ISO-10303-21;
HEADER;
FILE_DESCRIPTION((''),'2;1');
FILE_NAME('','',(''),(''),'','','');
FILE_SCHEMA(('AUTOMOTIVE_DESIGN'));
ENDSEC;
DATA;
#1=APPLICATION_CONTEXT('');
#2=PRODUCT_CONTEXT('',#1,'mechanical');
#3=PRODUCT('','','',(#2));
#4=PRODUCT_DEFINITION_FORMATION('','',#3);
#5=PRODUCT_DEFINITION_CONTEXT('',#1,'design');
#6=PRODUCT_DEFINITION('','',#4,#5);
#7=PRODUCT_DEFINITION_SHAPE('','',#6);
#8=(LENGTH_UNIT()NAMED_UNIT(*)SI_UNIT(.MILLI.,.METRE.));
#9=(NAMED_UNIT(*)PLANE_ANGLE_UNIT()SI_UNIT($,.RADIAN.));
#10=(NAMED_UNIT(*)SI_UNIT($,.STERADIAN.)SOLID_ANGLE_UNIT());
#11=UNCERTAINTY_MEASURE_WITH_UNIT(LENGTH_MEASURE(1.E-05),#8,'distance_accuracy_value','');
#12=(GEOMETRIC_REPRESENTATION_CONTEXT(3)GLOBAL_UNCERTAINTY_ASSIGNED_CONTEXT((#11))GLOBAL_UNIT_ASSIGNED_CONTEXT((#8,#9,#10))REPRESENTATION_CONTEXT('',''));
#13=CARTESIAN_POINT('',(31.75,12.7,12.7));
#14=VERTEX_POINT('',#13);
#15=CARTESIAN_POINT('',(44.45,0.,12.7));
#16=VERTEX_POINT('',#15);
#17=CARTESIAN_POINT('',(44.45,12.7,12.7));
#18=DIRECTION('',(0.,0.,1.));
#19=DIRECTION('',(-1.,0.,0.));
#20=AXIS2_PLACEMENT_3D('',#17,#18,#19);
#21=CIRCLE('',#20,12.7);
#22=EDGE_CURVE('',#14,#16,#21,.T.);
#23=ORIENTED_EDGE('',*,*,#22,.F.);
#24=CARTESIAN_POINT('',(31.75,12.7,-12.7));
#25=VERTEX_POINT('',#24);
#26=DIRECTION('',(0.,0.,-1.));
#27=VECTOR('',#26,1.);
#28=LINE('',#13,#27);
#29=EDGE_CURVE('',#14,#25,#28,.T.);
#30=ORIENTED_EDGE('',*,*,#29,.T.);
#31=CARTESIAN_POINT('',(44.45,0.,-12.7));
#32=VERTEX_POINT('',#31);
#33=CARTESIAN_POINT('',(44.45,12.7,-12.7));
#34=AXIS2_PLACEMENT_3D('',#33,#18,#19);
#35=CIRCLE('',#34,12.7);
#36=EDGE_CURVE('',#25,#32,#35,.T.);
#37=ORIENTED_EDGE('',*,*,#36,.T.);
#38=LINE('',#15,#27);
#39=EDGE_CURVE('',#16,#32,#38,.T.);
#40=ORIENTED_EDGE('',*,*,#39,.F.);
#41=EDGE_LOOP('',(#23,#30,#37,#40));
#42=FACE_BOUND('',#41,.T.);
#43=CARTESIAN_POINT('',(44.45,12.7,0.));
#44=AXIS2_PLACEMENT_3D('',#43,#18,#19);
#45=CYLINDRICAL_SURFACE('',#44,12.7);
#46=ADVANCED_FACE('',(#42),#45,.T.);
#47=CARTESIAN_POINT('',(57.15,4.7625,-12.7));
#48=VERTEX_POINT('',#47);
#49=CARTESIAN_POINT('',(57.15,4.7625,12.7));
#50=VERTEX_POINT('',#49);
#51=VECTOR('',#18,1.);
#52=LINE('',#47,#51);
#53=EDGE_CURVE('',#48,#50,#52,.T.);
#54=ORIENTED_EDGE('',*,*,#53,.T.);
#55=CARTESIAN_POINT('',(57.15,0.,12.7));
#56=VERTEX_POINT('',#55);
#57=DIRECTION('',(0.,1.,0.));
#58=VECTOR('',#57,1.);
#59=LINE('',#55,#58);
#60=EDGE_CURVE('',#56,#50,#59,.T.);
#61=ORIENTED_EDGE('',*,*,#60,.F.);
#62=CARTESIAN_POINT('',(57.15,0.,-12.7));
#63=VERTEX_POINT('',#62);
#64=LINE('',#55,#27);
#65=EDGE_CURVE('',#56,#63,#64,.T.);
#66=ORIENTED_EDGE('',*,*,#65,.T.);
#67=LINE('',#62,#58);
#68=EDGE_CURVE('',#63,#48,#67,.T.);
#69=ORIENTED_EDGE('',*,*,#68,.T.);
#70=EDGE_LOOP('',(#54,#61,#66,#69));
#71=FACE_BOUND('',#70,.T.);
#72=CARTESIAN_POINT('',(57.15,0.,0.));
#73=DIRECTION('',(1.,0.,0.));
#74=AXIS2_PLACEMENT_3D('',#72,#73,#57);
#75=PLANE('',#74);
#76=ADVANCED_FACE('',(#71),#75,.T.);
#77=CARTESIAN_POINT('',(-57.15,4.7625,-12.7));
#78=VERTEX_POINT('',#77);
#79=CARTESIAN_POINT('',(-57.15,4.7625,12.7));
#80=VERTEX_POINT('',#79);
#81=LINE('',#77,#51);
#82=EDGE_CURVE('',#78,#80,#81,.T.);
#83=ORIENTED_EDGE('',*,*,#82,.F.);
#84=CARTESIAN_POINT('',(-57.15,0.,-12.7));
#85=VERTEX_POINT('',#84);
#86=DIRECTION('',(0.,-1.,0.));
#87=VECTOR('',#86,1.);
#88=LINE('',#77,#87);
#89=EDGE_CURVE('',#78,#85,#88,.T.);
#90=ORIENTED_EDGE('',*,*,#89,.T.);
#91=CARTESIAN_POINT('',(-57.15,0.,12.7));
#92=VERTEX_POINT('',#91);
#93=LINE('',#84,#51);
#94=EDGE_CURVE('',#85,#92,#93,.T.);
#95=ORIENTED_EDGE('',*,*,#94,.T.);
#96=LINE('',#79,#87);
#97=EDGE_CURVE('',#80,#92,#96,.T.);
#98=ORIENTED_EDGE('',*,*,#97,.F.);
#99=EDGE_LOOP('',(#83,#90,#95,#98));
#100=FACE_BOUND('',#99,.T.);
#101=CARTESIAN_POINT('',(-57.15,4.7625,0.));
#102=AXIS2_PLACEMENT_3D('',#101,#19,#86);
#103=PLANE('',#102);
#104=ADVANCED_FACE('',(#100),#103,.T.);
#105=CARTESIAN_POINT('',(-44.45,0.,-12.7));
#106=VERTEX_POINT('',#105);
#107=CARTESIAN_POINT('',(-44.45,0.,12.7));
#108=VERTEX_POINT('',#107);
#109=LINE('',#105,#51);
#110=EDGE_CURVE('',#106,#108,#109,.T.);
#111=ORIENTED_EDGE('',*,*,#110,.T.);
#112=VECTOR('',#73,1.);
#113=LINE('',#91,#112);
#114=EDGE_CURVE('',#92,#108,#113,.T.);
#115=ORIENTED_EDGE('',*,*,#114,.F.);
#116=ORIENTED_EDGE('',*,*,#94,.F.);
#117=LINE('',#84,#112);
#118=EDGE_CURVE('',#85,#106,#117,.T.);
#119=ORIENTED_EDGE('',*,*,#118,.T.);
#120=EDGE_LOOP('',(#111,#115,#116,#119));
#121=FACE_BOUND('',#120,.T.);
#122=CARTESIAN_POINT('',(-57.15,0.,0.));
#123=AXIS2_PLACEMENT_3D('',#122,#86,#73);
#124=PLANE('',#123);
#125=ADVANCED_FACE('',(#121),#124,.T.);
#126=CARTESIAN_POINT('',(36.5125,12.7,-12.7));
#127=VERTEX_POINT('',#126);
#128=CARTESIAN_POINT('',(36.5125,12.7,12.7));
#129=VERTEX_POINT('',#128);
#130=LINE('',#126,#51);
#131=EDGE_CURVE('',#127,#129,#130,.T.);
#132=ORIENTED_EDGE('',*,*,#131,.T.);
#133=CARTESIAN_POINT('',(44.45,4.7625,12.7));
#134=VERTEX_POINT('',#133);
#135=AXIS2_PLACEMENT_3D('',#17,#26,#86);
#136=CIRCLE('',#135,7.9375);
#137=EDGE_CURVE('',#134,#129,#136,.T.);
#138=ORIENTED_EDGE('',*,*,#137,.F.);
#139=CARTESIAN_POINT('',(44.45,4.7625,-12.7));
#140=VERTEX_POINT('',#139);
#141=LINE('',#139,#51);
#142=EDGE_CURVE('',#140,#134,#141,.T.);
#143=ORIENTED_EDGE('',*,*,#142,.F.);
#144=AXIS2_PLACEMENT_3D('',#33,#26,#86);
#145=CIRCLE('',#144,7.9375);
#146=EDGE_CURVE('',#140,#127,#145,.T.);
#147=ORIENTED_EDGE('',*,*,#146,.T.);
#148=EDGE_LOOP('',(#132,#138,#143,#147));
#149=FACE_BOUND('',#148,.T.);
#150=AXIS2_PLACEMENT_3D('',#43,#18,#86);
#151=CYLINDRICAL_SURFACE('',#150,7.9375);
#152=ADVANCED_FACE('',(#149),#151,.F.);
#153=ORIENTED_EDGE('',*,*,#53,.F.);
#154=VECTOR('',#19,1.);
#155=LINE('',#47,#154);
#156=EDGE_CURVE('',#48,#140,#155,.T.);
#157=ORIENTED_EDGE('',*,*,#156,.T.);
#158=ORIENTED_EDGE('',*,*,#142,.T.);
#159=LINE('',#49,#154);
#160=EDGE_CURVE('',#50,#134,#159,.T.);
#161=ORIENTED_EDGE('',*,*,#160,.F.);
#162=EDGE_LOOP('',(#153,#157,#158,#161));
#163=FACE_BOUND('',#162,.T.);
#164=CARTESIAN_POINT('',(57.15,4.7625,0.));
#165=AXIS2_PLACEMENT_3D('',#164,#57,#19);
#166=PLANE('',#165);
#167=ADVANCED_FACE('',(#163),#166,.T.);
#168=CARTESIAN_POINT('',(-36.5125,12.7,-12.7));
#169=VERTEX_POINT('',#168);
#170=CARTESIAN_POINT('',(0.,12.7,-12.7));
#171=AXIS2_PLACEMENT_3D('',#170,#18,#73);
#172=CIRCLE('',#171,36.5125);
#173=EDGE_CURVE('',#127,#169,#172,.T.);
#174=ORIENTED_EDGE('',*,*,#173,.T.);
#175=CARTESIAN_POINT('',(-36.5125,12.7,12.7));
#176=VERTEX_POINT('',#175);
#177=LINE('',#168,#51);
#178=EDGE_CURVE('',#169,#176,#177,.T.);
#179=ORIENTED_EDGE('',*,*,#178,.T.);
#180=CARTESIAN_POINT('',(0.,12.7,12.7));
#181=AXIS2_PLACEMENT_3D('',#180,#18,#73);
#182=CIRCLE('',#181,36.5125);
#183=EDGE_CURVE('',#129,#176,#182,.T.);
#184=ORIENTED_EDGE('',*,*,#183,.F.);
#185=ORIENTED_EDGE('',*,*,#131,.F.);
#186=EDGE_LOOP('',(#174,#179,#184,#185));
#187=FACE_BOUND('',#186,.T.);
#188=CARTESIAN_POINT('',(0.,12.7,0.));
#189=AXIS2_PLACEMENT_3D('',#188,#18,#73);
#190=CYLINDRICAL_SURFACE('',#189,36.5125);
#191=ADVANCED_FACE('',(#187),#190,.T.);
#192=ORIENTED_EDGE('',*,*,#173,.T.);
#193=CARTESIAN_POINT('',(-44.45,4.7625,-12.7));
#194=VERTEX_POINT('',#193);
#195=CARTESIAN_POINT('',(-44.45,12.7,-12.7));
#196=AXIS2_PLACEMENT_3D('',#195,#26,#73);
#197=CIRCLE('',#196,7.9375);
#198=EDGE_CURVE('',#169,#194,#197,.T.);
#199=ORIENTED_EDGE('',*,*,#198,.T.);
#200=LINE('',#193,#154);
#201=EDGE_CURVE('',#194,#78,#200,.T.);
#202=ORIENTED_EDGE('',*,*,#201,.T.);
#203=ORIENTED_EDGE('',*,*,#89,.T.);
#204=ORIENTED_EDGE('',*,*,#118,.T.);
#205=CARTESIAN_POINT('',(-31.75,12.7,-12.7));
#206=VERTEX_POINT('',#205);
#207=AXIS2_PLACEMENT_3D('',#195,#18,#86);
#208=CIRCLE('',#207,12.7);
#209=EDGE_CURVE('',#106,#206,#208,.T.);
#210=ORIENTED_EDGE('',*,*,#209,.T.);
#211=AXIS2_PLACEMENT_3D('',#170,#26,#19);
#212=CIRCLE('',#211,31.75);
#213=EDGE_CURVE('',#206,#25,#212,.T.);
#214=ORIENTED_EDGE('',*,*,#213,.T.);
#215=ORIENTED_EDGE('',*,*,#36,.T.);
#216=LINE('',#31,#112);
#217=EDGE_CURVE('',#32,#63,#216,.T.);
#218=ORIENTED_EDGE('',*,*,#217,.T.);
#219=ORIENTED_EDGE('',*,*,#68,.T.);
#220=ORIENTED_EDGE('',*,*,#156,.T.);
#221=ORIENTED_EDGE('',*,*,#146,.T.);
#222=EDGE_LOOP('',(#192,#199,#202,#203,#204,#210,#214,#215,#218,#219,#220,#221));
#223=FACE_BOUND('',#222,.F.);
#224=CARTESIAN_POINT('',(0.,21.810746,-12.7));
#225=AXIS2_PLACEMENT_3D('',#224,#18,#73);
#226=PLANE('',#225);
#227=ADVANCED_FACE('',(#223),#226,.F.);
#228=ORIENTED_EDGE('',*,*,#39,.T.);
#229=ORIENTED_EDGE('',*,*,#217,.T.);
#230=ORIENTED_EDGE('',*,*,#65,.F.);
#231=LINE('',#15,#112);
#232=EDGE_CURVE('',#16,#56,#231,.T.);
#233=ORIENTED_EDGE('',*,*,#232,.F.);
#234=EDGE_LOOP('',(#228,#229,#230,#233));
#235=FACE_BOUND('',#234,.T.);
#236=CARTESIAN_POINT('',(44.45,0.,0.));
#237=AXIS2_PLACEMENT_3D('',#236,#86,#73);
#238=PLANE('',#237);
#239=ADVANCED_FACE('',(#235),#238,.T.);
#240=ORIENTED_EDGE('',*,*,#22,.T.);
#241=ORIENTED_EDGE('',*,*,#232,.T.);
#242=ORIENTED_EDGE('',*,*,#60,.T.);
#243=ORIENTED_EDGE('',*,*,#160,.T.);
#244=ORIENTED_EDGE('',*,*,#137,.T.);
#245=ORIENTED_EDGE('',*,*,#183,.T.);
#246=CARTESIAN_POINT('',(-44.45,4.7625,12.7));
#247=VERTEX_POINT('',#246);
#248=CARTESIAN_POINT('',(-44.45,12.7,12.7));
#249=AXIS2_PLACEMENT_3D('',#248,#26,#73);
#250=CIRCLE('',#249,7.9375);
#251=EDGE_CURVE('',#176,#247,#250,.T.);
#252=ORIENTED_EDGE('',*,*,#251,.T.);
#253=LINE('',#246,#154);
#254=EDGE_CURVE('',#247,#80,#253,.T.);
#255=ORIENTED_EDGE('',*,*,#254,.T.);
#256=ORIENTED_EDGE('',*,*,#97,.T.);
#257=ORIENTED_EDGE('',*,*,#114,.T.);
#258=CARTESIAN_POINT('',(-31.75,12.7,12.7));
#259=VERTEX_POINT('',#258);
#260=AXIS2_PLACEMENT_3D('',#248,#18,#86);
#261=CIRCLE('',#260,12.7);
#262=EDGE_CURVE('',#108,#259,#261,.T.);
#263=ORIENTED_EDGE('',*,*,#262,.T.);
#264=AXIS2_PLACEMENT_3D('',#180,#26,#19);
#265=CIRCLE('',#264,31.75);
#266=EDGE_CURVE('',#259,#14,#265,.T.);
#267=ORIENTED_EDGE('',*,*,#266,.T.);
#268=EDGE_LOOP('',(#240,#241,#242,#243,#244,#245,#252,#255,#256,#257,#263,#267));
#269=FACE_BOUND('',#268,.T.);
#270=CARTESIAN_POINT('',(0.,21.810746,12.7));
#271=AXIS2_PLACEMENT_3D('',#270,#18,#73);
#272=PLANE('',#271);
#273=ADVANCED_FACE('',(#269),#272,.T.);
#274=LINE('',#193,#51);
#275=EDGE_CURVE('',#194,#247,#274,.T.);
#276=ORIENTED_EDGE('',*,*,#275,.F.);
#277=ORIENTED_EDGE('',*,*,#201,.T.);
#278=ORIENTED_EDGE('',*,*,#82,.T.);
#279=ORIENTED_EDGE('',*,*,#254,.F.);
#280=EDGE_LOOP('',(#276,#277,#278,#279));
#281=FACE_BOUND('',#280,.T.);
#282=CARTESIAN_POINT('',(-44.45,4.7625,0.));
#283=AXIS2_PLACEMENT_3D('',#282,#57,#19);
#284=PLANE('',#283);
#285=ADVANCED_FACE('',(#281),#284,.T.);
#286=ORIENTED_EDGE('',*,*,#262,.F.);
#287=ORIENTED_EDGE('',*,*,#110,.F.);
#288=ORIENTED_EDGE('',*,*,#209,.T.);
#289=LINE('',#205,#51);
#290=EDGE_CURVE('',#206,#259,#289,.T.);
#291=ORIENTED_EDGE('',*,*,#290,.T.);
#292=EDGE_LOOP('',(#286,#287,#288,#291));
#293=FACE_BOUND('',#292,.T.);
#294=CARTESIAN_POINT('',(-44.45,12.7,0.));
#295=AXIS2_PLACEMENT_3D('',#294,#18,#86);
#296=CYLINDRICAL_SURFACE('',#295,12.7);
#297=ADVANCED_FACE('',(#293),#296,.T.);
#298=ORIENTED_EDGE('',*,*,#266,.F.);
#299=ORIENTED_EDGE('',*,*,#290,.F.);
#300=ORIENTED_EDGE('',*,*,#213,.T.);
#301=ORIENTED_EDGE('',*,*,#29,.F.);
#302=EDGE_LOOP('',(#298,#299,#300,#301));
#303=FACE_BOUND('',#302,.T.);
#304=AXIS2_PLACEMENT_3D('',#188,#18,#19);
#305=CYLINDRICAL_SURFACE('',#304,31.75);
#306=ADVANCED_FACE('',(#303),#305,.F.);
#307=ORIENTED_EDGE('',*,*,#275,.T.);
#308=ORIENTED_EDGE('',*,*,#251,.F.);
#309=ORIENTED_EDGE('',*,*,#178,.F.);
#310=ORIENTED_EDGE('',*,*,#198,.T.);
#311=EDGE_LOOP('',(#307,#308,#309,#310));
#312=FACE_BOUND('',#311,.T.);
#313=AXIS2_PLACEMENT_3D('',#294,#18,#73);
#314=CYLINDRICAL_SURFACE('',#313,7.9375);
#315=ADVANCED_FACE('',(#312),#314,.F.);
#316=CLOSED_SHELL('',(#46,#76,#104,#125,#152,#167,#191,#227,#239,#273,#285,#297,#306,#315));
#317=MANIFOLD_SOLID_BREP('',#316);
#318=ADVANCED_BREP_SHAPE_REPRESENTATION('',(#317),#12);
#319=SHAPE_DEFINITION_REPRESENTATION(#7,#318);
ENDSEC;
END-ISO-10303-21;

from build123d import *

# Parameters (mm, degrees)
BOSS_EXTRUDE1_DEPTH = 12.7


with BuildPart() as part:
    # Sketch1 → Boss-Extrude1 (new, symmetric)
    with BuildSketch(Plane.XY):
        with BuildLine():
            Line((57.15, 0), (57.15, 4.7625))
            Line((57.15, 4.7625), (44.45, 4.7625))
            ThreePointArc((44.45, 4.7625), (38.837339924, 7.087339924), (36.5125, 12.7))
            ThreePointArc((36.5125, 12.7), (0, 49.2125), (-36.5125, 12.7))
            ThreePointArc((-36.5125, 12.7), (-38.837339924, 7.087339924), (-44.45, 4.7625))
            Line((-44.45, 4.7625), (-57.15, 4.7625))
            Line((-57.15, 4.7625), (-57.15, 0))
            Line((-57.15, 0), (-44.45, 0))
            ThreePointArc((-44.45, 0), (-35.469743879, 3.719743879), (-31.75, 12.7))
            ThreePointArc((-31.75, 12.7), (0, 44.45), (31.75, 12.7))
            ThreePointArc((31.75, 12.7), (35.469743879, 3.719743879), (44.45, 0))
            Line((44.45, 0), (57.15, 0))
        make_face()
    extrude(amount=BOSS_EXTRUDE1_DEPTH, both=True)


solid = part.part
